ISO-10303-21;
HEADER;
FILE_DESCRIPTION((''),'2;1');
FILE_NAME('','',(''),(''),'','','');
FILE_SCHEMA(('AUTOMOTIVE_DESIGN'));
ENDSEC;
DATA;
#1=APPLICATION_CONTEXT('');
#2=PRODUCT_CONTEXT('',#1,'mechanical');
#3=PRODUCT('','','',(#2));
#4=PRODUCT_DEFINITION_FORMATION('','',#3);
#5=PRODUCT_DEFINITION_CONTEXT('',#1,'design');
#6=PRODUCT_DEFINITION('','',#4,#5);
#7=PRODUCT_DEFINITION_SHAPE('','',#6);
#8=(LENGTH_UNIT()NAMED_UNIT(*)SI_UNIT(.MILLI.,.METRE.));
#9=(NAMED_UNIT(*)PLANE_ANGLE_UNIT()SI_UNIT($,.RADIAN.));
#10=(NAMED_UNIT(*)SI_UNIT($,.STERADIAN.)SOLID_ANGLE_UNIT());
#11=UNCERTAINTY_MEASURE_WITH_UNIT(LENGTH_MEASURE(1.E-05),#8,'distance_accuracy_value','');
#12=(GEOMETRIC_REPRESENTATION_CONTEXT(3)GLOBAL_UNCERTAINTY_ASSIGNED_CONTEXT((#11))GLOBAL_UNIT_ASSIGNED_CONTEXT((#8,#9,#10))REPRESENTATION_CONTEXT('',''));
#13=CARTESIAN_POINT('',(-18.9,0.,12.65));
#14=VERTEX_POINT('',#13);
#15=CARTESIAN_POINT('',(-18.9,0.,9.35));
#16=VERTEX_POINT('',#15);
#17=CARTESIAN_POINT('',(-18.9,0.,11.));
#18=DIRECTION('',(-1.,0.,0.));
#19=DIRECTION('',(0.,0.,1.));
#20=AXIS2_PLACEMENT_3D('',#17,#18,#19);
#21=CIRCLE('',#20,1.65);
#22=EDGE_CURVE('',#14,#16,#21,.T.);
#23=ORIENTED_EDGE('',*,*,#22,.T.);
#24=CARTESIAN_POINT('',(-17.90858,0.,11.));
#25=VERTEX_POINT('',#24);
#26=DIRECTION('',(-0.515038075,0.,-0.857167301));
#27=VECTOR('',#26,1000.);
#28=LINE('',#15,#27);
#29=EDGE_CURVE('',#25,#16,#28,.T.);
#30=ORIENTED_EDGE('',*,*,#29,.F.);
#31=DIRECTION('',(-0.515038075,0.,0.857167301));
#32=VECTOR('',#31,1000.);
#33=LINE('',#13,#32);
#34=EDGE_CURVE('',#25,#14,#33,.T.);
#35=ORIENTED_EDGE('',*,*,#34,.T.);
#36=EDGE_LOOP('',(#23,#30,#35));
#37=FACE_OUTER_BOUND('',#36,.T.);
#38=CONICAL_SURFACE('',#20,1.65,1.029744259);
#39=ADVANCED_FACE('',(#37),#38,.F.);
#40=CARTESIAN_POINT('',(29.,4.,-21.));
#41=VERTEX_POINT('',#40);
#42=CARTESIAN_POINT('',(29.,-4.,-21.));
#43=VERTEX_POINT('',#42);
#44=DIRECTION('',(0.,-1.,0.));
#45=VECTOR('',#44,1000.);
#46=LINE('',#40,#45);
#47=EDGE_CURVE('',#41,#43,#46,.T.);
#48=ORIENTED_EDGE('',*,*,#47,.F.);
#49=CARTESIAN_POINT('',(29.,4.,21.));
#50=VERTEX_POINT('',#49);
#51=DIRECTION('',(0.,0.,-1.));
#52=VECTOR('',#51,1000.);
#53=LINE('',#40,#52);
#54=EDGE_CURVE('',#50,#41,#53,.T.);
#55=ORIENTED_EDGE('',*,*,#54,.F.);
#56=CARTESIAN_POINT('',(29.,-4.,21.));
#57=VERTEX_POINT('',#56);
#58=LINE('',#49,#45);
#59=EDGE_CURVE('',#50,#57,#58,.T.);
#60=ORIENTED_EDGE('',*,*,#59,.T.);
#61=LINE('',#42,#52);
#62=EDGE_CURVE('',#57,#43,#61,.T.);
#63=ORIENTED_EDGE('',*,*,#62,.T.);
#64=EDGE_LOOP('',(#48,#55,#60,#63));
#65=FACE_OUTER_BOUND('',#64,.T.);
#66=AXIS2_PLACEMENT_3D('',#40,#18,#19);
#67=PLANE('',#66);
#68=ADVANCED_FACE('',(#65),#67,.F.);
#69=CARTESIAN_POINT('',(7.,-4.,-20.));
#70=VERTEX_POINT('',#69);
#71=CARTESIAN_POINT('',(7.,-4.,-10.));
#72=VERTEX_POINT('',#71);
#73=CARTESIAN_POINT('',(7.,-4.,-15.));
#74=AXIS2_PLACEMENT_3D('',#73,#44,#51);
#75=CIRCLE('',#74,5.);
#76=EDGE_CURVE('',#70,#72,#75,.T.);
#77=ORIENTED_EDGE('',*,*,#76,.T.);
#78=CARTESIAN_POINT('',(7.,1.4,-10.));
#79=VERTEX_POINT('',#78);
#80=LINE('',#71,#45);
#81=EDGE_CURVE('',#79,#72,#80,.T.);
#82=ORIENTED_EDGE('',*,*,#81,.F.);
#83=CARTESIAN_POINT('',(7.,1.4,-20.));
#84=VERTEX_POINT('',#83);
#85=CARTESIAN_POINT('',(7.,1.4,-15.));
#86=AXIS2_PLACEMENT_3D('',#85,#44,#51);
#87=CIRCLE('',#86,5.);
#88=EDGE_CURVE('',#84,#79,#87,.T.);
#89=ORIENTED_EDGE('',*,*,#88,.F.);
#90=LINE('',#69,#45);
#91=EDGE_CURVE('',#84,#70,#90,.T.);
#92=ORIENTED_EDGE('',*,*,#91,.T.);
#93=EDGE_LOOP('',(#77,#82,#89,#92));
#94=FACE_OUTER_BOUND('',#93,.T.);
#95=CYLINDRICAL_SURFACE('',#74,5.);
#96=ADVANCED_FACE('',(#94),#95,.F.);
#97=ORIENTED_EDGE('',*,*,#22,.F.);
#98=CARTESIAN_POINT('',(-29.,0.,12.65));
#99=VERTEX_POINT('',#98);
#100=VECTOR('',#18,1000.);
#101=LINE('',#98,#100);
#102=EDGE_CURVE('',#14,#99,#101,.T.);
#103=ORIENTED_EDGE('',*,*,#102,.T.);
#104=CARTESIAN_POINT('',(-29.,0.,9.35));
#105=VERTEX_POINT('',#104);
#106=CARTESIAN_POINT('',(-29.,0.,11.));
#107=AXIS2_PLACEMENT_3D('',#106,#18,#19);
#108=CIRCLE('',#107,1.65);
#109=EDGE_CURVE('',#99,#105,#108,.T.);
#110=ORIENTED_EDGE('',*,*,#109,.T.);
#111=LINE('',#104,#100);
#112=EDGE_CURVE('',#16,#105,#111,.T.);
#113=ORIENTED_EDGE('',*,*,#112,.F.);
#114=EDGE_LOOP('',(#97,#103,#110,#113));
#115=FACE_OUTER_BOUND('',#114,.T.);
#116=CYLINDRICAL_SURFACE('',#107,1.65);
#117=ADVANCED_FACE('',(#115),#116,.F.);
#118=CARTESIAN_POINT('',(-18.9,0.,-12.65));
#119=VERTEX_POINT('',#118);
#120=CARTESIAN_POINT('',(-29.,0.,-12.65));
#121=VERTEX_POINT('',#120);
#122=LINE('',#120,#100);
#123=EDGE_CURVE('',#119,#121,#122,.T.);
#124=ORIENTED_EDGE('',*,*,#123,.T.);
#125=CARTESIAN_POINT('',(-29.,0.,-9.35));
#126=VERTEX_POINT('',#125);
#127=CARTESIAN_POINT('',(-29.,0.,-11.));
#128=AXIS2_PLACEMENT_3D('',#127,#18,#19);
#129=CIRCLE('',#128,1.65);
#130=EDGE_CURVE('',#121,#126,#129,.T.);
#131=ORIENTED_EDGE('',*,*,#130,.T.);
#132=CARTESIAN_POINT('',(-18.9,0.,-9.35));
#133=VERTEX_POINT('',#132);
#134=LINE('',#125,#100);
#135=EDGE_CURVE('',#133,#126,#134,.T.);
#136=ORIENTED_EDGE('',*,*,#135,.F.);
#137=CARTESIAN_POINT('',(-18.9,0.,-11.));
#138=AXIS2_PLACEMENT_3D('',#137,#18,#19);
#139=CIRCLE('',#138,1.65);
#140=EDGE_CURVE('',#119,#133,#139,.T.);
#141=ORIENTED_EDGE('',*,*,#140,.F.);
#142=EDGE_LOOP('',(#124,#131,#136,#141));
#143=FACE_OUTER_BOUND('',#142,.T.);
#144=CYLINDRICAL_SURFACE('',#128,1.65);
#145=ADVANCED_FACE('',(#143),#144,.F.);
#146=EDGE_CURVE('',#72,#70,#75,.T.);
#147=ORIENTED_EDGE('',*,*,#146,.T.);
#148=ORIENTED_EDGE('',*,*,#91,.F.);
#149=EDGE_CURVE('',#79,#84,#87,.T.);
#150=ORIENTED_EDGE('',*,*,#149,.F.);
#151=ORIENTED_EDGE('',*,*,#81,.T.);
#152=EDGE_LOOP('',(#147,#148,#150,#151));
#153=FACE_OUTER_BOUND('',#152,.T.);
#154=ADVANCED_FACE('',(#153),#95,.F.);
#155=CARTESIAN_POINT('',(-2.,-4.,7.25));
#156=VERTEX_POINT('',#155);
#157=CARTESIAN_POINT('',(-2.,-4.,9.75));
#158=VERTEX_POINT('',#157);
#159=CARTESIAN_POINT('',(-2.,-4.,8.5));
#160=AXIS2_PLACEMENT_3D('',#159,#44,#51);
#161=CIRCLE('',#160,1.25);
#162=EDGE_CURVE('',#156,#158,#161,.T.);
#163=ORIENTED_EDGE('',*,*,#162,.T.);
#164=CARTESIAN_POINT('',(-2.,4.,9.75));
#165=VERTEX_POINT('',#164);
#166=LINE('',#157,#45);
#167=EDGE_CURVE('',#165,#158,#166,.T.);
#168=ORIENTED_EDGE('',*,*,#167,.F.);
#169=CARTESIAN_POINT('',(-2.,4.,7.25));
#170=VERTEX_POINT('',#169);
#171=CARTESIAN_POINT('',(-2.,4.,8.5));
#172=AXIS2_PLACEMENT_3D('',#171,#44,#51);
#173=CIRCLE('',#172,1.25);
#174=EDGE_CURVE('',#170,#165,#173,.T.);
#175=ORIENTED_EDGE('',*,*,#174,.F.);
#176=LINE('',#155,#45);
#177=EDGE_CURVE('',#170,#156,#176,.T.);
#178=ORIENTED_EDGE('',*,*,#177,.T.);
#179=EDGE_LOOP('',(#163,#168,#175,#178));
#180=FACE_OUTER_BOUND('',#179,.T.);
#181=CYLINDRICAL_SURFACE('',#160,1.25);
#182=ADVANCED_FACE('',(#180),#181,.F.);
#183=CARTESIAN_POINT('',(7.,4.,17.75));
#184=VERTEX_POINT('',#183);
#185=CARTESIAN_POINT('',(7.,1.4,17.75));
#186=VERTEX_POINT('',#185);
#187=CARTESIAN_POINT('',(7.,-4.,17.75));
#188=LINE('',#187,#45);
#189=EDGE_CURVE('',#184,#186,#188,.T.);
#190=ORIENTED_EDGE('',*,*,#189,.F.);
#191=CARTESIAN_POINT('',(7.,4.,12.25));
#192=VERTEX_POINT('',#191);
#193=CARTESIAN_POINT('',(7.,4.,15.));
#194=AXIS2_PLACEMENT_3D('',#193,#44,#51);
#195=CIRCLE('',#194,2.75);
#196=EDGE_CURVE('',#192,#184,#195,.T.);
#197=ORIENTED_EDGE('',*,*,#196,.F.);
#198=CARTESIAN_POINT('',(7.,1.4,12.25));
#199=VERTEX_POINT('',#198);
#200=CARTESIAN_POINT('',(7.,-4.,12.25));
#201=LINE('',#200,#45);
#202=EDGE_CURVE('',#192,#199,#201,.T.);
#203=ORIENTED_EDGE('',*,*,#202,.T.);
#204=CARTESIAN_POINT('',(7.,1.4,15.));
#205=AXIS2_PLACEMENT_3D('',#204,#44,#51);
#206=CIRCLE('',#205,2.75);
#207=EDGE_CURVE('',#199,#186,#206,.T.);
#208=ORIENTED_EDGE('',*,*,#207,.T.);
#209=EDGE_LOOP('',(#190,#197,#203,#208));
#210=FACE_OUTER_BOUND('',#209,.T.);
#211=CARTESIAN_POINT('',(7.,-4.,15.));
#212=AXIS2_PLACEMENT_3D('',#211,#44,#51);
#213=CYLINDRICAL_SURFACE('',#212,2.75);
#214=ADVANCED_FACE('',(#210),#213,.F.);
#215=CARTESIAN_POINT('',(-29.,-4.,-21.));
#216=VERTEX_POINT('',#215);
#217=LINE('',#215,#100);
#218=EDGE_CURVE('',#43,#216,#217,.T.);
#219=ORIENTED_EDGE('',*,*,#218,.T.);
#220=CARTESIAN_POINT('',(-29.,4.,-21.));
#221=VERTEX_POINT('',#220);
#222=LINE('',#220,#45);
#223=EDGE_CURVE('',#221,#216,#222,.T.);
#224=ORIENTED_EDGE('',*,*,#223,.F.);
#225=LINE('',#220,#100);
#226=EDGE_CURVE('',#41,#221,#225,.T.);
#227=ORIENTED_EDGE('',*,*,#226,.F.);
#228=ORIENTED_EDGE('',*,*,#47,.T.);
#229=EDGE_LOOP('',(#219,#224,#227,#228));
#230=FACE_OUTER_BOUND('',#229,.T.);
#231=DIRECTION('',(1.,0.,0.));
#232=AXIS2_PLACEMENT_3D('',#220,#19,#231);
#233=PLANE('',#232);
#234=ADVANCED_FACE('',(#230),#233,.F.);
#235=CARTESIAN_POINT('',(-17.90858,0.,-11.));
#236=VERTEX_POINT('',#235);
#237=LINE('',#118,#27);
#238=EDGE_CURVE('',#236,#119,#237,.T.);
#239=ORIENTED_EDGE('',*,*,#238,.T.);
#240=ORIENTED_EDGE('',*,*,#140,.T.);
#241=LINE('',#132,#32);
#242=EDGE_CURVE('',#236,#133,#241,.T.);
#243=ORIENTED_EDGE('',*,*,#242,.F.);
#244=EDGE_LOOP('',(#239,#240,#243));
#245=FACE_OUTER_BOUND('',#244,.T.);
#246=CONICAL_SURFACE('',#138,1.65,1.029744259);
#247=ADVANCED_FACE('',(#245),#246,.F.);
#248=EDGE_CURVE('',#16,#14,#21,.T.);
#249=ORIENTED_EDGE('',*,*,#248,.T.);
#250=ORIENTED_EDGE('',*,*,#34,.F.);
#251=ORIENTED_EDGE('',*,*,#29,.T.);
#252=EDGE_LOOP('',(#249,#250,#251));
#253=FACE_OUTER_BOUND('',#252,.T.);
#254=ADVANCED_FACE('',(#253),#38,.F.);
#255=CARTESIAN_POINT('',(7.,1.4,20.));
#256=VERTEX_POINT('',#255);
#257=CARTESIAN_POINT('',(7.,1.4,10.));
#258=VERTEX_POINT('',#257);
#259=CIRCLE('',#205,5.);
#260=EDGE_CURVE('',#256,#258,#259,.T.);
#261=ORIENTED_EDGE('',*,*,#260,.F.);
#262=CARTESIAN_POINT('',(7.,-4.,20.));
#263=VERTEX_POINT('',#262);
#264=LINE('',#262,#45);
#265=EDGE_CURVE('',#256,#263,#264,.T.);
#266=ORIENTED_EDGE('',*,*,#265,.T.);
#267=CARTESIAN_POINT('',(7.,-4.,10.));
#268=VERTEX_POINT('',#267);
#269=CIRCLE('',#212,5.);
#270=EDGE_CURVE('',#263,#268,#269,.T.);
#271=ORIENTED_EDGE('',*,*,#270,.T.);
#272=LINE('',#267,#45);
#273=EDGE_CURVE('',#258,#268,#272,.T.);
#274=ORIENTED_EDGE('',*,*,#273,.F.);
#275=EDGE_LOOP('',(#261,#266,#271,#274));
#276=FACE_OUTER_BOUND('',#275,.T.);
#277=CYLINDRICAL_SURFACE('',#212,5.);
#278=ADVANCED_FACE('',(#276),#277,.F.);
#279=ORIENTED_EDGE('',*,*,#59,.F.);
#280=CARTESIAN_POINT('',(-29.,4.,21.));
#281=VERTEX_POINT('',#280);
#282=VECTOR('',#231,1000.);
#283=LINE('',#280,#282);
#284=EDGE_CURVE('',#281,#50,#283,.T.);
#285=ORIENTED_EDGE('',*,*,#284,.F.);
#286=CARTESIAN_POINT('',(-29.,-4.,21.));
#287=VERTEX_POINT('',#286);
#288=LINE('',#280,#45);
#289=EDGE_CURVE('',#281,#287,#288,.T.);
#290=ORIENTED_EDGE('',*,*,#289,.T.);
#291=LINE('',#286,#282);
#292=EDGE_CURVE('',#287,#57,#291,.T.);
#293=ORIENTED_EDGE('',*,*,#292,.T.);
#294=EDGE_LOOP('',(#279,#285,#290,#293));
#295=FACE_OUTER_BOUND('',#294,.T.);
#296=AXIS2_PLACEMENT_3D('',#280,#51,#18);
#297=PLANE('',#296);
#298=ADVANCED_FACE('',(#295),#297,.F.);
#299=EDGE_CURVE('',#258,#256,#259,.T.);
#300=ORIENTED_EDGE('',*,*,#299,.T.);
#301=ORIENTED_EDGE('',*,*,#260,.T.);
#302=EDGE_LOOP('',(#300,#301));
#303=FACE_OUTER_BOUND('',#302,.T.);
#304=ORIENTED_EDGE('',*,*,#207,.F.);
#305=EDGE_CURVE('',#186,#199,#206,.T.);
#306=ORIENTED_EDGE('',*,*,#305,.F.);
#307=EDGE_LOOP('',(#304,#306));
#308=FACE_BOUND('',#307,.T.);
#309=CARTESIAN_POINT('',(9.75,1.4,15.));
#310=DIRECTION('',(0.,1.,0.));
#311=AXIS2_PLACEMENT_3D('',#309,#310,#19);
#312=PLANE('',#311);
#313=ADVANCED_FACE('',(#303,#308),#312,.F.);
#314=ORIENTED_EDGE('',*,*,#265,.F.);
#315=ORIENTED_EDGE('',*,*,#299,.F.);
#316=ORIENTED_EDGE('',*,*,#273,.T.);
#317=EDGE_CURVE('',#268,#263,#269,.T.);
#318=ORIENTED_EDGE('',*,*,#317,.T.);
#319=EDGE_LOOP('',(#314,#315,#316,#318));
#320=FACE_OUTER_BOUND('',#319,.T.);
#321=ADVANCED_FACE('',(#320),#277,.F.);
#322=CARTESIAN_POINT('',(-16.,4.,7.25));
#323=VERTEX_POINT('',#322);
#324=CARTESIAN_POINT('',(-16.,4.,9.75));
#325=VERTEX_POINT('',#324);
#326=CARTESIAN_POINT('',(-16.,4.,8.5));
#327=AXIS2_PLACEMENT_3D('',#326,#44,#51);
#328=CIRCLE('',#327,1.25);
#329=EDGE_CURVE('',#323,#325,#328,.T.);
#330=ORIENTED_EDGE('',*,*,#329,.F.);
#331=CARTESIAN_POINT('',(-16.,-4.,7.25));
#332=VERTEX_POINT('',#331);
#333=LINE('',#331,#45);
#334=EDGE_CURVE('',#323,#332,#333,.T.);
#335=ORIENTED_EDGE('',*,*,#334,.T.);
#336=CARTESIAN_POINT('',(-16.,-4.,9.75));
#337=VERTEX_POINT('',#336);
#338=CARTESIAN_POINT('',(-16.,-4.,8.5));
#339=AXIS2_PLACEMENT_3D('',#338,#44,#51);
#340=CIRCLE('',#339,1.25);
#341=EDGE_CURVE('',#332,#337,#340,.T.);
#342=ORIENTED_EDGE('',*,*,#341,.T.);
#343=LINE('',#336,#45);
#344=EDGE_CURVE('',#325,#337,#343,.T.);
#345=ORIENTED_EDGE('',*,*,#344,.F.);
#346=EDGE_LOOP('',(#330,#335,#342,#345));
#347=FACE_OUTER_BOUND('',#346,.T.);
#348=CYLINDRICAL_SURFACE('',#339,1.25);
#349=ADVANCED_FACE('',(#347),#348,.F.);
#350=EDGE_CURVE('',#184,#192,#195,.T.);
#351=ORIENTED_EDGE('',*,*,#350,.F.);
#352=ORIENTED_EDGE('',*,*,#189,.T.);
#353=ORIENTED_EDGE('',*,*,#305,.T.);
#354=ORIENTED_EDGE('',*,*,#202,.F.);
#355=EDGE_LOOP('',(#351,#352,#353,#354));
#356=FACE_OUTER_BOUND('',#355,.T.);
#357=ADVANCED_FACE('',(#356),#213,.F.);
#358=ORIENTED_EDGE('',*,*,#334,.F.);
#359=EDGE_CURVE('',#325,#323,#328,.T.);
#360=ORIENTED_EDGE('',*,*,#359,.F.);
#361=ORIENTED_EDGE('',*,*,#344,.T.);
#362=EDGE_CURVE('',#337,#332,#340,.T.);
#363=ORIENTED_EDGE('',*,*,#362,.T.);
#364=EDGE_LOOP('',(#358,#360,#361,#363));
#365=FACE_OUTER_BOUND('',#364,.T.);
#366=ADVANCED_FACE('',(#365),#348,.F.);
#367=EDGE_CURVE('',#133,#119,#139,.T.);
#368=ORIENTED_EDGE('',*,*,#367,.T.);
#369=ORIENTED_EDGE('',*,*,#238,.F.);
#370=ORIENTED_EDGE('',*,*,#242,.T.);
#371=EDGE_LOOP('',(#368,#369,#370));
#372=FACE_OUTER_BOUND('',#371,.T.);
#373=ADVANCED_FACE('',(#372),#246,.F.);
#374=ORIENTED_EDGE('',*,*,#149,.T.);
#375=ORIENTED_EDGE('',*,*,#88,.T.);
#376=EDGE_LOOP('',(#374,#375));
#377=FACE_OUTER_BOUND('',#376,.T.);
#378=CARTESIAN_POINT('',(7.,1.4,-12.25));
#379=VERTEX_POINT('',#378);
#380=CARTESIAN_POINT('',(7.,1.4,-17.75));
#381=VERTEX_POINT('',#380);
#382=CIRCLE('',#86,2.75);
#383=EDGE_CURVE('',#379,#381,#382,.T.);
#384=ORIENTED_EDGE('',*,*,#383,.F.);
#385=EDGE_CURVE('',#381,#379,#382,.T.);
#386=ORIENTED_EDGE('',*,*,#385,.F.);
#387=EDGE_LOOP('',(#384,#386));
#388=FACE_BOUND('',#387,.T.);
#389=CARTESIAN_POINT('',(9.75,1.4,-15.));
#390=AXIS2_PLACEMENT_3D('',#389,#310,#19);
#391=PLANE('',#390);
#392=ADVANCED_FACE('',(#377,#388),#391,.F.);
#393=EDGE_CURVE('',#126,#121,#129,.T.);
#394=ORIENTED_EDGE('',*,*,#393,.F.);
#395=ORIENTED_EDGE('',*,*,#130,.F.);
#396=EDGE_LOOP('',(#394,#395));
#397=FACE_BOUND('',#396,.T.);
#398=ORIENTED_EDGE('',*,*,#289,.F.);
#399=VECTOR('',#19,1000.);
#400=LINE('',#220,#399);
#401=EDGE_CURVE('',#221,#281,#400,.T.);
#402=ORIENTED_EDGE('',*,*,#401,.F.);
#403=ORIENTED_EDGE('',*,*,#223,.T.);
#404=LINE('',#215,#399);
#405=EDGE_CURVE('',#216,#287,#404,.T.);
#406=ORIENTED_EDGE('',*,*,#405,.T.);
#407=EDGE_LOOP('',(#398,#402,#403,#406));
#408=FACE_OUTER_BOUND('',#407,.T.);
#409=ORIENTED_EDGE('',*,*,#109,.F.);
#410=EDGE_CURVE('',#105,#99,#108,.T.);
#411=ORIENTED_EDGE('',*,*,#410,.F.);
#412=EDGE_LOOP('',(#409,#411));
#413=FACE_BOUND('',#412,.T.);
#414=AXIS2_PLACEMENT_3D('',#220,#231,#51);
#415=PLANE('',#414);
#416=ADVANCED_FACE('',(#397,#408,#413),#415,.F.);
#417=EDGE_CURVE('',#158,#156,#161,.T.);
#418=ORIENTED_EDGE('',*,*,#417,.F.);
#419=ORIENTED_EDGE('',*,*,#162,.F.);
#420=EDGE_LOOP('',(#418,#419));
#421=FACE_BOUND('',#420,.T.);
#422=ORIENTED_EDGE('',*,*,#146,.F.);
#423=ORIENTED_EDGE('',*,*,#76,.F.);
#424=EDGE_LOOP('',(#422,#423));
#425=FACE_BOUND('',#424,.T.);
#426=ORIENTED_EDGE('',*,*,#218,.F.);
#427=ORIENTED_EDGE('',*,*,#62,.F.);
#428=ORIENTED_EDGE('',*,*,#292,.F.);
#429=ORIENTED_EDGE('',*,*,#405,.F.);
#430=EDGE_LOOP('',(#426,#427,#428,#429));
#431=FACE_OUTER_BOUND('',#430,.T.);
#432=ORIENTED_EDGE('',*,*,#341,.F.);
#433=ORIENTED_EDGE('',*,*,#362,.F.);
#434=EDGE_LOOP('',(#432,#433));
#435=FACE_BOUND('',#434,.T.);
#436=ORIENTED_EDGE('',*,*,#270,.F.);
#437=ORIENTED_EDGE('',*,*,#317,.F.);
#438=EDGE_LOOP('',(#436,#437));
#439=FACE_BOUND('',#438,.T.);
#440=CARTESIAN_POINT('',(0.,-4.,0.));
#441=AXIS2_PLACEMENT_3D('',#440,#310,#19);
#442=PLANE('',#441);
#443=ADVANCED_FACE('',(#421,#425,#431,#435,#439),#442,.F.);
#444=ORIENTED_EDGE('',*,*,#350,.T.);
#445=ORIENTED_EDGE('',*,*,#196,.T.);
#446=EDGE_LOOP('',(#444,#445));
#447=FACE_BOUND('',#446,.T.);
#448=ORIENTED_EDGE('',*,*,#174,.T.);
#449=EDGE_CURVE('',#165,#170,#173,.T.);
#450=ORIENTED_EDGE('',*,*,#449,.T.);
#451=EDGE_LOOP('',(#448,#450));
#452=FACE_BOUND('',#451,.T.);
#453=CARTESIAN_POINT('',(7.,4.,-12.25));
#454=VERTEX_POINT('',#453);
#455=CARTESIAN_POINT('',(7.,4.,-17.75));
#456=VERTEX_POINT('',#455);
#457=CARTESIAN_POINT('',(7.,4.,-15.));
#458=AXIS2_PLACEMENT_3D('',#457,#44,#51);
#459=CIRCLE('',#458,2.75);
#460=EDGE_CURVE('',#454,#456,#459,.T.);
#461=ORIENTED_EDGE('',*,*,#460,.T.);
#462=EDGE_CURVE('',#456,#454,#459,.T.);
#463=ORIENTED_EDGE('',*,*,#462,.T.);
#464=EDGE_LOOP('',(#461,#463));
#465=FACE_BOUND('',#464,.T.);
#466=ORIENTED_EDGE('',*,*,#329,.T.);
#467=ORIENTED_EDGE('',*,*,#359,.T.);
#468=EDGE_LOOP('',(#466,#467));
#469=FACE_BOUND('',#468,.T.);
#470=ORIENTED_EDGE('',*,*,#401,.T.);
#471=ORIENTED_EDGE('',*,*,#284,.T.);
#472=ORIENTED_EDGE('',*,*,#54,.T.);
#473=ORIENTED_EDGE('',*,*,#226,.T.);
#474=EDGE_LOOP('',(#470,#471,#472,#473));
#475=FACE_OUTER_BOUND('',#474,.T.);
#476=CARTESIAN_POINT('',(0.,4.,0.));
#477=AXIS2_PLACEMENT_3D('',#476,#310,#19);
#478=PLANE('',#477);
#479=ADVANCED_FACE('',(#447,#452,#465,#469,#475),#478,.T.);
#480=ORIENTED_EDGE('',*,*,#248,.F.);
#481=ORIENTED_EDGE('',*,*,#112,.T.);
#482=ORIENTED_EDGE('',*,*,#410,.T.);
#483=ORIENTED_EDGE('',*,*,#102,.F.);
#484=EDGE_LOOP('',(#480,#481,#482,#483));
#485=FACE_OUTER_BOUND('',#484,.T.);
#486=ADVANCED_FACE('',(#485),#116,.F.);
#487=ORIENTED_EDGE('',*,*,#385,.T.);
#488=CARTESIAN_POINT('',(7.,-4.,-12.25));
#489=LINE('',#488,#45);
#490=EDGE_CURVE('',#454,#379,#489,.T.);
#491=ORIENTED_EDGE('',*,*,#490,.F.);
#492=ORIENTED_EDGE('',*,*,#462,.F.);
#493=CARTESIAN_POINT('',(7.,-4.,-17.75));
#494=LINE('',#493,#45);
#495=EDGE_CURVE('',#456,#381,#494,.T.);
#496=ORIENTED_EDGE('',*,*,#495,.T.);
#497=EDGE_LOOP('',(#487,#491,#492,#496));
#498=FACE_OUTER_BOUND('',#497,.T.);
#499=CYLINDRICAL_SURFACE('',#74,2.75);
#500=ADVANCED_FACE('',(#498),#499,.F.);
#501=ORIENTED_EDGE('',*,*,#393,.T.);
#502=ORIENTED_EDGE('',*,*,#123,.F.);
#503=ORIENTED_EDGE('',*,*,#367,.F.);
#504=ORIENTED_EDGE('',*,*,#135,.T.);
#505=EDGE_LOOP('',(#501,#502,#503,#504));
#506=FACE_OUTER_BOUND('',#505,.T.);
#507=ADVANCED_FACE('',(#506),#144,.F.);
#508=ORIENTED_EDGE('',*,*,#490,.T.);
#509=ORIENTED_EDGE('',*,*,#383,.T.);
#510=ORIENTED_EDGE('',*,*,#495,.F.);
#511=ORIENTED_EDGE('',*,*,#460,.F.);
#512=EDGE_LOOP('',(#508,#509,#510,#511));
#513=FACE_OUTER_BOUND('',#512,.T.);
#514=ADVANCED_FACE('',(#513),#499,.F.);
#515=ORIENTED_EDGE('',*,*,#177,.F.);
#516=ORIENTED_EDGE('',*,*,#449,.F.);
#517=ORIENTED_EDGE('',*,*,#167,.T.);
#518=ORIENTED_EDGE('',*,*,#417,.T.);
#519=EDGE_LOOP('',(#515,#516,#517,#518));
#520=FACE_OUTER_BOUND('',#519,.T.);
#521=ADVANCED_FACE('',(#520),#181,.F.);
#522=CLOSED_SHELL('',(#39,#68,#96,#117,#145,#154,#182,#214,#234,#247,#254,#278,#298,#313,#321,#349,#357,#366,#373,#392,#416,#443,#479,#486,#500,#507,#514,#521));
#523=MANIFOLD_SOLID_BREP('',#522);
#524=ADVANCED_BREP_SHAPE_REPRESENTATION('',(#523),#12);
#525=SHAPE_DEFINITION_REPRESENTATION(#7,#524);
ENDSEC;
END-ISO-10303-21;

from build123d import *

# Parameters (mm, degrees)
SKETCH_1_W                   = 58
SKETCH_1_H                   = 42
EXTRUDE_1_DEPTH              = 4
HOLE_WIZARD_M5_1_D           = 5.5
HOLE_WIZARD_M5_1_CBORE_D     = 10
HOLE_WIZARD_M5_1_CBORE_DEPTH = 5.4
HOLE_WIZARD_M4_1_D           = 3.3
HOLE_WIZARD_M4_1_DEPTH       = 10.1
HOLE_WIZARD_M4_1_TIP         = 0.991420021
HOLE_WIZARD_M3_1_D           = 2.5


with BuildPart() as part:
    # 草图1 → 凸台-拉伸1 (new, symmetric)
    with BuildSketch(Plane(origin=(0, 0, 0), x_dir=(1, 0, 0), z_dir=(0, 1, 0))):
        Rectangle(SKETCH_1_W, SKETCH_1_H)
    extrude(amount=EXTRUDE_1_DEPTH, both=True)

    # M5 六角凹头螺钉的柱形沉头孔1 (through all)
    with Locations(Plane(origin=(0, -4, 0), x_dir=(-1, 0, 0), z_dir=(0, -1, 0))):
        with Locations((-7, 15), (-7, -15)):
            CounterBoreHole(HOLE_WIZARD_M5_1_D / 2, HOLE_WIZARD_M5_1_CBORE_D / 2, HOLE_WIZARD_M5_1_CBORE_DEPTH)

    # M4 螺纹孔1
    with Locations(Plane.ZY.offset(29)):
        with Locations((-11, 0), (11, 0)):
            Hole(HOLE_WIZARD_M4_1_D / 2, depth=HOLE_WIZARD_M4_1_DEPTH)
            with Locations((0, 0, -(HOLE_WIZARD_M4_1_DEPTH + HOLE_WIZARD_M4_1_TIP / 2))):  # 118° drill point
                Cone(0, HOLE_WIZARD_M4_1_D / 2, HOLE_WIZARD_M4_1_TIP, mode=Mode.SUBTRACT)

    # M3 螺纹孔1 (through all)
    with Locations(Plane(origin=(0, -4, 0), x_dir=(-1, 0, 0), z_dir=(0, -1, 0))):
        with Locations((16, -8.5), (2, -8.5)):
            Hole(HOLE_WIZARD_M3_1_D / 2)


solid = part.part
